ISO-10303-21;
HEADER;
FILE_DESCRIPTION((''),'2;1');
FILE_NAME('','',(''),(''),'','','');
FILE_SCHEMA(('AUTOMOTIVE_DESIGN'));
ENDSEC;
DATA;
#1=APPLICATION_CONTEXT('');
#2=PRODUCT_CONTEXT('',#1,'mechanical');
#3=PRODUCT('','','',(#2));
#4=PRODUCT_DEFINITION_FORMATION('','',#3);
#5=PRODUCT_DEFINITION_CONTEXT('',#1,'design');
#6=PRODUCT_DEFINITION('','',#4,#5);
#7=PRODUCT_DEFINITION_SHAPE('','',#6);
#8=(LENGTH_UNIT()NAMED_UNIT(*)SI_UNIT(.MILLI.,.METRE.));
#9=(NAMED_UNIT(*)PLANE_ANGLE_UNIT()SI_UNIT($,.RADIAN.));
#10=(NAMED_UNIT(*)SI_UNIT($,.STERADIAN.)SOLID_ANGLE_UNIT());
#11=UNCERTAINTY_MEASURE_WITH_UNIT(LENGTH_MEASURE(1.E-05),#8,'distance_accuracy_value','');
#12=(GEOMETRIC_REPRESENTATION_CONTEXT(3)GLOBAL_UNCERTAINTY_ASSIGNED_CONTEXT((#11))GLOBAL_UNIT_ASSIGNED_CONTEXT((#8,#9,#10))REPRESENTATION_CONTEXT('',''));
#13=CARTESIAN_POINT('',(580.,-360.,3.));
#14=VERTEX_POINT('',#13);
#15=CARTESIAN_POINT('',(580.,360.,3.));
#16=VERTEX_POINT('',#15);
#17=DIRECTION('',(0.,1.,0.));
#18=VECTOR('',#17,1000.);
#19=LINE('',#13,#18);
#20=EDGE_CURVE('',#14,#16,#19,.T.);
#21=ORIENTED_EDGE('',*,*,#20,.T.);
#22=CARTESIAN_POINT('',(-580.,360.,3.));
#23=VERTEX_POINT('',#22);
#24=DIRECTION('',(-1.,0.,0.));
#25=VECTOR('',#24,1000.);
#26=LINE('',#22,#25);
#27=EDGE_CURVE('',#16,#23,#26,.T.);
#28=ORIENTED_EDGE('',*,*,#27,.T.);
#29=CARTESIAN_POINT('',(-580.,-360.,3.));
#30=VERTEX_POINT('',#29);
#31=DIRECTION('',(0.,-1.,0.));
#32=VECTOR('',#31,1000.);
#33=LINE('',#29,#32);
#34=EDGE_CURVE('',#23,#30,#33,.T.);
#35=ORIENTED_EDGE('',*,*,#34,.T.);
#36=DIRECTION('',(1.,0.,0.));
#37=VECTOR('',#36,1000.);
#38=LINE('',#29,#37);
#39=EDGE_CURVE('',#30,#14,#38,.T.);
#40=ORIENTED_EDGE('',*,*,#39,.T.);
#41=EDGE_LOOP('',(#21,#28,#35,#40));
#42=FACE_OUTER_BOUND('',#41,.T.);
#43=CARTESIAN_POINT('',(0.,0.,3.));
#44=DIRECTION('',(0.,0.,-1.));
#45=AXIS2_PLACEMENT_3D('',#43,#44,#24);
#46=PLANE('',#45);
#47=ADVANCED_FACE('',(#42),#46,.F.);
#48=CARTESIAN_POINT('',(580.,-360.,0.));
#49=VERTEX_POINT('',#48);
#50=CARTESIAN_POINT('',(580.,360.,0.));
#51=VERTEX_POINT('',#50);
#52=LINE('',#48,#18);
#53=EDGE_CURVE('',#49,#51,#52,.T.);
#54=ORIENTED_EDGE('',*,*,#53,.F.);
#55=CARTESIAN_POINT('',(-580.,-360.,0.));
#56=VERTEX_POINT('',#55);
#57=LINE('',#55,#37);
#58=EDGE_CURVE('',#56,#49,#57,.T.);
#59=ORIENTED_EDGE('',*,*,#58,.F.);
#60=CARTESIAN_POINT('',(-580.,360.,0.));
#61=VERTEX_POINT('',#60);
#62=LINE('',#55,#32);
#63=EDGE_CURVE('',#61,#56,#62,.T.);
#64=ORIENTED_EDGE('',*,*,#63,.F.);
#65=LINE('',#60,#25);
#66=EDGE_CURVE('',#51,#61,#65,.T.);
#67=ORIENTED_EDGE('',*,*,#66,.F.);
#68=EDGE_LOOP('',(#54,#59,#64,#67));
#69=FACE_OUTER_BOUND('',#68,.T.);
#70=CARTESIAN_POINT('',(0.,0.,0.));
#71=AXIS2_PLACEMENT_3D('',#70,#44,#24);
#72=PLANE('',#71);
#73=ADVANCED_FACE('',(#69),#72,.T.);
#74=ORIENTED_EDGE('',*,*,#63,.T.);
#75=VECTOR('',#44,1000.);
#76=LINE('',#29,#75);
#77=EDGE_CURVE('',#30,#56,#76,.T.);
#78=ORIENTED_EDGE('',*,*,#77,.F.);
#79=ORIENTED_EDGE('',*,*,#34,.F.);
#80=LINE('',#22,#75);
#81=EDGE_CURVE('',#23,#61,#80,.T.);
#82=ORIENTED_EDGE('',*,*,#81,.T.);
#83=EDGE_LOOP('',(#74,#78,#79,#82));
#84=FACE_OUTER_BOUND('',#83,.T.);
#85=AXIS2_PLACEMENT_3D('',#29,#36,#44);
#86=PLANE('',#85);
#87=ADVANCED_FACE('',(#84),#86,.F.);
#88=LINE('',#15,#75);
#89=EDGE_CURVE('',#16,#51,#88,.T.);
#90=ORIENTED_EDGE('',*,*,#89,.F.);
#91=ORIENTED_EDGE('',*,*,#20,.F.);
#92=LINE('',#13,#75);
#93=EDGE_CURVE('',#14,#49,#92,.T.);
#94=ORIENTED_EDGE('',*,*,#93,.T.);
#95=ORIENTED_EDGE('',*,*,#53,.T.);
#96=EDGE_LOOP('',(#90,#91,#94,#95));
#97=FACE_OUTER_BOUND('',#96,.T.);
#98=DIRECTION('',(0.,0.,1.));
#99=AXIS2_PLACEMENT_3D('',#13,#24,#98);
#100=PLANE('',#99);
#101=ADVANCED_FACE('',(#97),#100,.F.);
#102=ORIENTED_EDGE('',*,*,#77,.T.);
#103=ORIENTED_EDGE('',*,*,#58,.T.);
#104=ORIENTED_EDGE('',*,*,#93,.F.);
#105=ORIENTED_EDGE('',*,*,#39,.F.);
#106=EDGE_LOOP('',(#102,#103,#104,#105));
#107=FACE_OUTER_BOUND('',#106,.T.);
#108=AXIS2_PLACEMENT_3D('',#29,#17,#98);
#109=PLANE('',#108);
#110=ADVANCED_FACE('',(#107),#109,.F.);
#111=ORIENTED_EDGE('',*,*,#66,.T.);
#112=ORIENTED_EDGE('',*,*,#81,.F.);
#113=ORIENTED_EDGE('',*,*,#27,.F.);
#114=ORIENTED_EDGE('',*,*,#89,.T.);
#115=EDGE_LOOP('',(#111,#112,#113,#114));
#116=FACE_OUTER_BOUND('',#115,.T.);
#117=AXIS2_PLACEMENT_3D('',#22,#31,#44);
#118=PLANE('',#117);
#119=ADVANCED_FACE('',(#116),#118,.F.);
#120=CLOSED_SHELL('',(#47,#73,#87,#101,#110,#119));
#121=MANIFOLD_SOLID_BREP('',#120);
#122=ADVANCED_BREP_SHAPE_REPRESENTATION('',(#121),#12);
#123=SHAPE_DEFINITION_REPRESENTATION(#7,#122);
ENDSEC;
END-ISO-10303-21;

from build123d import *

# Parameters (mm, degrees)
SKETCH_1_W      = 1160
SKETCH_1_H      = 720
EXTRUDE_1_DEPTH = 3


with BuildPart() as part:
    # 草图1 → 凸台-拉伸1 (new body)
    with BuildSketch(Plane.XY):
        Rectangle(SKETCH_1_W, SKETCH_1_H)
    extrude(amount=EXTRUDE_1_DEPTH)


solid = part.part
